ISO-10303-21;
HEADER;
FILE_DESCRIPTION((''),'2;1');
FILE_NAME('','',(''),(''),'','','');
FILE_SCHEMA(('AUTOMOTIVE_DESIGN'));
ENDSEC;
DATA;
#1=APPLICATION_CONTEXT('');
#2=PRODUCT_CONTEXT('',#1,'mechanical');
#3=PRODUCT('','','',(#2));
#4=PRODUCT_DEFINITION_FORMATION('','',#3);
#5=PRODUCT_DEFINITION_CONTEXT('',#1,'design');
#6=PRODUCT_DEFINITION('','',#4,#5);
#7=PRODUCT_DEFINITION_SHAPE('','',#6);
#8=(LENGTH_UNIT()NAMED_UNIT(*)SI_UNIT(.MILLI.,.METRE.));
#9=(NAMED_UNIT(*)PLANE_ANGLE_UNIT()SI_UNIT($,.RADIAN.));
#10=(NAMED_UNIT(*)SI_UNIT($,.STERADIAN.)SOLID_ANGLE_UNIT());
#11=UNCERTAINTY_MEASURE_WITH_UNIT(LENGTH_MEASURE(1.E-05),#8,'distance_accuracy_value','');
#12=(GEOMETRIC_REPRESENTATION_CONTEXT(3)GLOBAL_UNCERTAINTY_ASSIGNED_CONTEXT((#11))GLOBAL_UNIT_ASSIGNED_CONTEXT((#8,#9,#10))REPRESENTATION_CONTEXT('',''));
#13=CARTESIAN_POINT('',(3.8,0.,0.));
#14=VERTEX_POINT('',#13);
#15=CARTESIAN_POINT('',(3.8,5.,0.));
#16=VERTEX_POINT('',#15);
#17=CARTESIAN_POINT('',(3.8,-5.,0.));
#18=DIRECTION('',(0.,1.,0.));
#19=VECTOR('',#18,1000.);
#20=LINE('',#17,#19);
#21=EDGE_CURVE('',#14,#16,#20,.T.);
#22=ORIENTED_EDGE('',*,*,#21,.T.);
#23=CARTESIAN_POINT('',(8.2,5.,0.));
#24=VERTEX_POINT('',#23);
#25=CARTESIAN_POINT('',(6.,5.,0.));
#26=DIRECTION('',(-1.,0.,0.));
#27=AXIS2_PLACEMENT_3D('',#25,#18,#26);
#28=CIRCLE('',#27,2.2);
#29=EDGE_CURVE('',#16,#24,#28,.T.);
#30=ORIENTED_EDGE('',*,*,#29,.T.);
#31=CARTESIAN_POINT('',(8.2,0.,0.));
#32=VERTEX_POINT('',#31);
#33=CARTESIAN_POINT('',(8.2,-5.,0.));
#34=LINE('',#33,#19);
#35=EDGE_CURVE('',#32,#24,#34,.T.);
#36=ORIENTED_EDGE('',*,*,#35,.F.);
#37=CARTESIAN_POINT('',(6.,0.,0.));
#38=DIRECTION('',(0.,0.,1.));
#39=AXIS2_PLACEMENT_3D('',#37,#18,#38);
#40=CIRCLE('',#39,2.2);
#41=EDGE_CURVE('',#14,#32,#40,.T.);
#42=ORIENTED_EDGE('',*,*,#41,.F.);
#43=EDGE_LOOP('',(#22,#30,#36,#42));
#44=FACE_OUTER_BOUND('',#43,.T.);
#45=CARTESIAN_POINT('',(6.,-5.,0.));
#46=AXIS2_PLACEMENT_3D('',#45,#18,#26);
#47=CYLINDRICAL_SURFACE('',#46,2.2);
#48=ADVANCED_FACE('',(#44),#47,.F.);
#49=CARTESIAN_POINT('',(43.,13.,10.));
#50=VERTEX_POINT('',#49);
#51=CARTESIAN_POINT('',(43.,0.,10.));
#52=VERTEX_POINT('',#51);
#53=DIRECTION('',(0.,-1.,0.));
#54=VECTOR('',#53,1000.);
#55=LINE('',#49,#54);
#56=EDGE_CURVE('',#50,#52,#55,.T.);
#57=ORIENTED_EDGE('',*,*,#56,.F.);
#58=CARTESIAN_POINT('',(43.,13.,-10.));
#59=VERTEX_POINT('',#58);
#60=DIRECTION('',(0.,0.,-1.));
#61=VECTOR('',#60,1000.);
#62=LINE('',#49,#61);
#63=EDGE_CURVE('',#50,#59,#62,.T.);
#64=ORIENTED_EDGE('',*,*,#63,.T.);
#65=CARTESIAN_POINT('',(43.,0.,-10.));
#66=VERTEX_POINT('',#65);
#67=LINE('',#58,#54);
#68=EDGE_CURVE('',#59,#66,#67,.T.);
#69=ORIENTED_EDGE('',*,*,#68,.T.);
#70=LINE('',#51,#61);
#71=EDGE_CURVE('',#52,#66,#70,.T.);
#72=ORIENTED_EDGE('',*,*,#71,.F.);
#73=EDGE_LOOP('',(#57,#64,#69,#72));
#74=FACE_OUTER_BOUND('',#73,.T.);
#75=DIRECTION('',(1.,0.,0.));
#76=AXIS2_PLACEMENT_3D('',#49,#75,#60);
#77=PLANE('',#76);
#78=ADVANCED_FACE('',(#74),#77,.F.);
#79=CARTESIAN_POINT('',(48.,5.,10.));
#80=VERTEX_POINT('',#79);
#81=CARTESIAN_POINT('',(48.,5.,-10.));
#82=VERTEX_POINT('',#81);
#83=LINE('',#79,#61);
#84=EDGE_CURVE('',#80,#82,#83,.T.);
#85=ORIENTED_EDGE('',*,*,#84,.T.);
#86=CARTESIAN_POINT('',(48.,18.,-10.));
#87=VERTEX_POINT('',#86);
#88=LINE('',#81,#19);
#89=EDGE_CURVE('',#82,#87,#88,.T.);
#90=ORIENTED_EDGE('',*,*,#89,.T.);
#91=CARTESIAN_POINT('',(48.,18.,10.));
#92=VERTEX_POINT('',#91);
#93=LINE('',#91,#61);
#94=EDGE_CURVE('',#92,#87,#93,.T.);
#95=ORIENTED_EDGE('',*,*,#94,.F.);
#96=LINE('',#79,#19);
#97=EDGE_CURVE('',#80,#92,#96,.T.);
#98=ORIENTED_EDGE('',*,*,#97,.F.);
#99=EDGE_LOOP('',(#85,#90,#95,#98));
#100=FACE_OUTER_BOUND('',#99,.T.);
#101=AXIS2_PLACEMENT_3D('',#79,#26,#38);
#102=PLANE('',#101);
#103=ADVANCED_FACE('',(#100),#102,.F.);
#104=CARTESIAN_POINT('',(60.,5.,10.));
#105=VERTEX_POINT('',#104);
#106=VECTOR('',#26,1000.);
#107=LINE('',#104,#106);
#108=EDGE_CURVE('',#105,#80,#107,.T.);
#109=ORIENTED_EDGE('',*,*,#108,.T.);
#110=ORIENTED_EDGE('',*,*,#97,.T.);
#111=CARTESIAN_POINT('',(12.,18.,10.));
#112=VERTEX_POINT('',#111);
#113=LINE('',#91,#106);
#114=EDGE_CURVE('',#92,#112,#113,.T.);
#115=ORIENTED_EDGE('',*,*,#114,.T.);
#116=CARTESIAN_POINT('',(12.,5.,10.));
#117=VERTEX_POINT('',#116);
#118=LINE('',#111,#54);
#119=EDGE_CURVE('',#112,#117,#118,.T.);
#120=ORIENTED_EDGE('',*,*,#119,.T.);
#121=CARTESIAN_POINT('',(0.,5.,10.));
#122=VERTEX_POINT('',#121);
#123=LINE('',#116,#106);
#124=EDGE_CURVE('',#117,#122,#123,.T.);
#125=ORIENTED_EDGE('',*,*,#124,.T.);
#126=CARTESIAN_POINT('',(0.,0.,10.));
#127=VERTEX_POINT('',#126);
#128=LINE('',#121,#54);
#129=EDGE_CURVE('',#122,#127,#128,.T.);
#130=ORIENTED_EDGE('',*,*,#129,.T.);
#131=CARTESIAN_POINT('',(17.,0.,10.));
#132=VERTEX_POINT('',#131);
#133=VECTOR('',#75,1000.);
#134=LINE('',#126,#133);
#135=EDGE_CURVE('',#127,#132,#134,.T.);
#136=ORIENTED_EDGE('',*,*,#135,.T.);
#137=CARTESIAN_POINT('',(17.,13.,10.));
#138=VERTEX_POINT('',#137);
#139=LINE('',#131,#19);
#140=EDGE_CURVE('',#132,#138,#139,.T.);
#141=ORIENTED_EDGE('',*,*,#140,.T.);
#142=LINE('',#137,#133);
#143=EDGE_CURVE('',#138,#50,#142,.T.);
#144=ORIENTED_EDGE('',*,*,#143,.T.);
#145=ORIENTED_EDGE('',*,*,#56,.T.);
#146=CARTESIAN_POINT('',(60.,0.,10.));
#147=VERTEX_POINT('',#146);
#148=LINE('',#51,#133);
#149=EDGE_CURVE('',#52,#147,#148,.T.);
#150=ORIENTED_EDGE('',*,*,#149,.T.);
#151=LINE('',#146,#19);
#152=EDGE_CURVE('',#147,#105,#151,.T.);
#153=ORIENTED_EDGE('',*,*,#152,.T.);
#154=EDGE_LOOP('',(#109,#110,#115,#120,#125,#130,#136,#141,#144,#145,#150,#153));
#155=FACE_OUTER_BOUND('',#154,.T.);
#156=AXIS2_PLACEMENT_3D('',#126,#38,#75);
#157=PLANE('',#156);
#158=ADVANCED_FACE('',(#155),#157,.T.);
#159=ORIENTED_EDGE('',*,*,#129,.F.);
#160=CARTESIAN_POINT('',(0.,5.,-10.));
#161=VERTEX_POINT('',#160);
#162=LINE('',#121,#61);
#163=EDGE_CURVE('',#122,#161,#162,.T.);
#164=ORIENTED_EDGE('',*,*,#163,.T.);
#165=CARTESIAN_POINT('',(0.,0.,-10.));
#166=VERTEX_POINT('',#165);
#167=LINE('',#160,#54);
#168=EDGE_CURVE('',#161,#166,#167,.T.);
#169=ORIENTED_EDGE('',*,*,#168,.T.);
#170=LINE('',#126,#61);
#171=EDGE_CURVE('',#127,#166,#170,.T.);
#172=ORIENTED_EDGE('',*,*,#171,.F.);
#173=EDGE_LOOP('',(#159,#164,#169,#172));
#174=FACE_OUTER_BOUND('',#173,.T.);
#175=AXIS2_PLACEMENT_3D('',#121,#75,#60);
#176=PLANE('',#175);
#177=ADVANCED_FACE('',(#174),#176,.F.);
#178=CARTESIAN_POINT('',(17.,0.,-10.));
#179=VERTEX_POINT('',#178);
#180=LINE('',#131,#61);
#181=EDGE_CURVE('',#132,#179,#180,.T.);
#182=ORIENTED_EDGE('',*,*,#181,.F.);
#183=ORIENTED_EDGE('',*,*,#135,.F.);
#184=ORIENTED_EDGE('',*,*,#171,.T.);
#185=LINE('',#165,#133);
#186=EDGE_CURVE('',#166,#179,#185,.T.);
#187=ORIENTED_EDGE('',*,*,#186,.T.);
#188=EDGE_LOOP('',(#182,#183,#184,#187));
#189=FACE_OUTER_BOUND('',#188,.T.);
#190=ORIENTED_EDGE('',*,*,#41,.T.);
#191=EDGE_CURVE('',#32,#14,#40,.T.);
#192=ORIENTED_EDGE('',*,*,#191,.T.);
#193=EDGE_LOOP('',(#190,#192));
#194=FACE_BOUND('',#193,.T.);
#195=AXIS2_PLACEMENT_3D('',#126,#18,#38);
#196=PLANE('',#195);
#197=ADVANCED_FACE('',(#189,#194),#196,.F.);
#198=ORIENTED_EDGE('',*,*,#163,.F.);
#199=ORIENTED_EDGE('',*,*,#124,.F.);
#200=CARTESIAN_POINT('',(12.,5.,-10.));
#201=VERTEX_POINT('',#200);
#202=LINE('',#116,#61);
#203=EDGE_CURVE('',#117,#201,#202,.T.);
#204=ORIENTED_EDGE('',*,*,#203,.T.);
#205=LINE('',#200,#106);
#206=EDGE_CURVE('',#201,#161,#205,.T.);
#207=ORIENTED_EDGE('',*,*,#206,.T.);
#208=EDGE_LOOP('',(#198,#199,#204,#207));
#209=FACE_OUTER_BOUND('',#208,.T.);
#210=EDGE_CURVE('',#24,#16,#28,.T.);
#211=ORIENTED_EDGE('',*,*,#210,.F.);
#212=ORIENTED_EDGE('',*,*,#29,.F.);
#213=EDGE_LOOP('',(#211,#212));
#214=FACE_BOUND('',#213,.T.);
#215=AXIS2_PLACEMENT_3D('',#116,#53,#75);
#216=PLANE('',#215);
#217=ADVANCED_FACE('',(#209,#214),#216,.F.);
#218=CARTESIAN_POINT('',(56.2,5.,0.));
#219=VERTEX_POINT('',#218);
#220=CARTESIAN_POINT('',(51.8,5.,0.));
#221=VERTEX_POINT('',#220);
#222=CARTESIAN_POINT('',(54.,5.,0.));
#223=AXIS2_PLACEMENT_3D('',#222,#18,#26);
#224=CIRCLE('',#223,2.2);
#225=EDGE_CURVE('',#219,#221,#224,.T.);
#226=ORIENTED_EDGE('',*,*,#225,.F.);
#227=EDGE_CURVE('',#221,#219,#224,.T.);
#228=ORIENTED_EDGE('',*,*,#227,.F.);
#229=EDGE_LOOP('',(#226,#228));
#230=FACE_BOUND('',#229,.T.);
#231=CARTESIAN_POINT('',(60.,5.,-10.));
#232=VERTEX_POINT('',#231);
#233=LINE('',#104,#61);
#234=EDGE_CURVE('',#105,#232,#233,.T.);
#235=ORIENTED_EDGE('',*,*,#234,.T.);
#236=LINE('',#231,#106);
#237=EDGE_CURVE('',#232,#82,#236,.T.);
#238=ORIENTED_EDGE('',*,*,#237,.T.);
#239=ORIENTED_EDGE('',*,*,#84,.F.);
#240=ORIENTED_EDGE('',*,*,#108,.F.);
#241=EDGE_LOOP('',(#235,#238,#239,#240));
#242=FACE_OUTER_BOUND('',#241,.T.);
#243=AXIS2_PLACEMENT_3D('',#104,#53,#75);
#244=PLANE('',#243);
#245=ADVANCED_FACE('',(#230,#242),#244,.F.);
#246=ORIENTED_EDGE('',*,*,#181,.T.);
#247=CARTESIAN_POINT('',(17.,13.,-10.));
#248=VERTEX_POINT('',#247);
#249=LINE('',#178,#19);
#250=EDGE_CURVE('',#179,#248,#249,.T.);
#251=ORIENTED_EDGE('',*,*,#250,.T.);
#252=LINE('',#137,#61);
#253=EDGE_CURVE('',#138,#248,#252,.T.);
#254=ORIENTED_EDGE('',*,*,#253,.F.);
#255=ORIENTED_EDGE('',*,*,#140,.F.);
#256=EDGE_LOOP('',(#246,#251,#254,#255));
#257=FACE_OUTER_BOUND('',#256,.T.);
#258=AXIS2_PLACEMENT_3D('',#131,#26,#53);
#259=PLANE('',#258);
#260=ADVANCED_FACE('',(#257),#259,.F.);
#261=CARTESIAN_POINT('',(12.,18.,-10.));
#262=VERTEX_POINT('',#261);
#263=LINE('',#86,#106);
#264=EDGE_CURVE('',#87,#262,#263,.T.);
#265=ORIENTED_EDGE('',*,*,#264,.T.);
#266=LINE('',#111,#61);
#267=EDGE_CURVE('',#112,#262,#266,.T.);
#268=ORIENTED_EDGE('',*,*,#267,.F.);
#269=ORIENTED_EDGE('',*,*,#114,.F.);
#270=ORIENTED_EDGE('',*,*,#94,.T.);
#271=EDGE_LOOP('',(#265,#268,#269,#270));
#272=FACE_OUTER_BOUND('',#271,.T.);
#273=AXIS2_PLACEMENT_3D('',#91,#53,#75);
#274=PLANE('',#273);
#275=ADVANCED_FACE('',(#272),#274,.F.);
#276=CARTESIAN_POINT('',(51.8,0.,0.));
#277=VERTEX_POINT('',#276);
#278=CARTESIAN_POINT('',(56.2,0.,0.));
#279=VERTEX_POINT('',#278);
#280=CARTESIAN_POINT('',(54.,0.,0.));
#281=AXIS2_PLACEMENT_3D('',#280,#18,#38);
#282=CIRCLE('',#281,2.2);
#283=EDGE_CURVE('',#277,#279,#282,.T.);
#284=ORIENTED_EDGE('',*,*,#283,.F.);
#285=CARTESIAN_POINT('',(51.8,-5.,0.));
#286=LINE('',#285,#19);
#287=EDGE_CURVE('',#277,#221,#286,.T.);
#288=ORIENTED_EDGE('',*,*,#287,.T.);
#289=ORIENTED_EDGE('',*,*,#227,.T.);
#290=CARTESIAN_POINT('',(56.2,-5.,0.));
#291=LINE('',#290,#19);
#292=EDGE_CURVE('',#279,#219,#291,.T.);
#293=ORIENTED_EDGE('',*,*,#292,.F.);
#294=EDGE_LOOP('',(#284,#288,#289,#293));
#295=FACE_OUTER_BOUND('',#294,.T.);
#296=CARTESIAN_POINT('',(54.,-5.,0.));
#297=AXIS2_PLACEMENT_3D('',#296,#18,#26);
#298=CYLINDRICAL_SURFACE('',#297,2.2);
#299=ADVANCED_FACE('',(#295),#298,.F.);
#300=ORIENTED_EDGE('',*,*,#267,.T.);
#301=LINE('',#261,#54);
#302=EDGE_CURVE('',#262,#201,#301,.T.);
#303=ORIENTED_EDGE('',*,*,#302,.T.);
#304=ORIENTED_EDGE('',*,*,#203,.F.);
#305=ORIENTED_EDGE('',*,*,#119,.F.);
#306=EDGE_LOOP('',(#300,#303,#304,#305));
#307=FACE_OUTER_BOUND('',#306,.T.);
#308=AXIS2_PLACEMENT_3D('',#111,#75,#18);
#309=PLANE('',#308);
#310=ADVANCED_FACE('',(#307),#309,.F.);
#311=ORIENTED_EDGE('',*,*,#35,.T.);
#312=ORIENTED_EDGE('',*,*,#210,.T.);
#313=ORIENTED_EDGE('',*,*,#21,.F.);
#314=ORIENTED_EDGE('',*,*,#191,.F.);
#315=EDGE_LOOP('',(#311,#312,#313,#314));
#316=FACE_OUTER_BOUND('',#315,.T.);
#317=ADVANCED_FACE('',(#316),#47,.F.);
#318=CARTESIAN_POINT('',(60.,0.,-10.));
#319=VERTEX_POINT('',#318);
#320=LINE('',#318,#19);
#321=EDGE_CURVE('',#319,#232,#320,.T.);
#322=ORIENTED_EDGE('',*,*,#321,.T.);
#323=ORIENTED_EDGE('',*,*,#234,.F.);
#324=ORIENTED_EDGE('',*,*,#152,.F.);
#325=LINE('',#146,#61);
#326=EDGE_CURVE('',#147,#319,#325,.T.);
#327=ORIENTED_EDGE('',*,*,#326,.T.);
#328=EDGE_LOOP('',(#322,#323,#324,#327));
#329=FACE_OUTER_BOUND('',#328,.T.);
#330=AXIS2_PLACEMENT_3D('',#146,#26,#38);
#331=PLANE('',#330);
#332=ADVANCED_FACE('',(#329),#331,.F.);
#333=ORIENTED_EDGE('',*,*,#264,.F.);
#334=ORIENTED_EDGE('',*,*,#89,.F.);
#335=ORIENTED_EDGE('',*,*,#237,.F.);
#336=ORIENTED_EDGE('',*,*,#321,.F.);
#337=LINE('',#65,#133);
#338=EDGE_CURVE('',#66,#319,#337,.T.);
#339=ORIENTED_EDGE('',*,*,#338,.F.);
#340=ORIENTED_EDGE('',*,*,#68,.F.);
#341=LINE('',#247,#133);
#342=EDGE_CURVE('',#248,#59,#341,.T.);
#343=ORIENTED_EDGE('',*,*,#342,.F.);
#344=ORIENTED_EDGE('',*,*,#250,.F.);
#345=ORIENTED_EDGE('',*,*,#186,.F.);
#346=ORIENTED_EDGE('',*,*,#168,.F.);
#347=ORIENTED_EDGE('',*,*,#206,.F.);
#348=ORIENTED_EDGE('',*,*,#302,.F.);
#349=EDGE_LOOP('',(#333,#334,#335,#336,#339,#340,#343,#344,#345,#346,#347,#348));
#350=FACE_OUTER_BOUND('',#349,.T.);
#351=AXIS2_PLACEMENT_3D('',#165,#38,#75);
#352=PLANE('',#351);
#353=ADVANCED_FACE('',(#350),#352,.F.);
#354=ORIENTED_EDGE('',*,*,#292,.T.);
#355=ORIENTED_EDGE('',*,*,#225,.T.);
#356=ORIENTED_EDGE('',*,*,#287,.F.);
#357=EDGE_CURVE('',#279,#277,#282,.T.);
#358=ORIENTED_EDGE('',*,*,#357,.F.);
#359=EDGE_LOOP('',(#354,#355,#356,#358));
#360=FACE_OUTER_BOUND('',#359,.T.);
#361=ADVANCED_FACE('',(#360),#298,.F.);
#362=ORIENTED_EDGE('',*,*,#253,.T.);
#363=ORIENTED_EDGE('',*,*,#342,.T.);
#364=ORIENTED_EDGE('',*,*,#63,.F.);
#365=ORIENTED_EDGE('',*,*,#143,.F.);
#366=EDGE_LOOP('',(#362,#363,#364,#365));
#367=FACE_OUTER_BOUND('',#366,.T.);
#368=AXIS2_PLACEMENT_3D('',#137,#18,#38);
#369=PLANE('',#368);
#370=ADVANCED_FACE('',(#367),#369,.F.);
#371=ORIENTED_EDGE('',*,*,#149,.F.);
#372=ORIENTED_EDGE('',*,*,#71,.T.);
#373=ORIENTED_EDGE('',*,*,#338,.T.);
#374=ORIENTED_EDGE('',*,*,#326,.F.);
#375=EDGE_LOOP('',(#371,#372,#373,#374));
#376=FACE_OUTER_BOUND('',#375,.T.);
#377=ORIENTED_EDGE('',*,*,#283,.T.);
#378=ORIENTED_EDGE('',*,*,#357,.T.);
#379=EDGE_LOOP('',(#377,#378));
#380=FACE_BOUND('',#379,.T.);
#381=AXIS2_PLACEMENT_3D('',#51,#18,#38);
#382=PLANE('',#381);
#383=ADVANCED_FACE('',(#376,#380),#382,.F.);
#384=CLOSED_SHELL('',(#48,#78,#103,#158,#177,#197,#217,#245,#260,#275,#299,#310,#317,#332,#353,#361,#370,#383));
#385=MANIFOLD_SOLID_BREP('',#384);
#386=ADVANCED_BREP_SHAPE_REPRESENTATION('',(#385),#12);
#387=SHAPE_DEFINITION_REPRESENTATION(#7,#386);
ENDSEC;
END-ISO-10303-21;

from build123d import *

# Parameters (mm, degrees)
EXTRUDE_1_DEPTH     = 10
SKETCH_2_R          = 2.2
CUT_EXTRUDE_1_DEPTH = 10


with BuildPart() as part:
    # 草图1 → 凸台-拉伸1 (new, symmetric)
    with BuildSketch(Plane.XY):
        Polygon((0, 0), (17, 0), (17, 13), (43, 13), (43, 0), (60, 0), (60, 5), (48, 5), (48, 18), (12, 18), (12, 5), (0, 5), align=None)
    extrude(amount=EXTRUDE_1_DEPTH, both=True)

    # 草图2 → 切除-拉伸1 (cut)
    with BuildSketch(Plane(origin=(0, 5, 0), x_dir=(1, 0, 0), z_dir=(0, 1, 0))):
        with Locations(Location((6, 0, 0), (0, 0, 180))):
            Circle(SKETCH_2_R)
        with Locations(Location((54, 0, 0), (0, 0, 180))):
            Circle(SKETCH_2_R)
    extrude(amount=-CUT_EXTRUDE_1_DEPTH, mode=Mode.SUBTRACT)


solid = part.part
